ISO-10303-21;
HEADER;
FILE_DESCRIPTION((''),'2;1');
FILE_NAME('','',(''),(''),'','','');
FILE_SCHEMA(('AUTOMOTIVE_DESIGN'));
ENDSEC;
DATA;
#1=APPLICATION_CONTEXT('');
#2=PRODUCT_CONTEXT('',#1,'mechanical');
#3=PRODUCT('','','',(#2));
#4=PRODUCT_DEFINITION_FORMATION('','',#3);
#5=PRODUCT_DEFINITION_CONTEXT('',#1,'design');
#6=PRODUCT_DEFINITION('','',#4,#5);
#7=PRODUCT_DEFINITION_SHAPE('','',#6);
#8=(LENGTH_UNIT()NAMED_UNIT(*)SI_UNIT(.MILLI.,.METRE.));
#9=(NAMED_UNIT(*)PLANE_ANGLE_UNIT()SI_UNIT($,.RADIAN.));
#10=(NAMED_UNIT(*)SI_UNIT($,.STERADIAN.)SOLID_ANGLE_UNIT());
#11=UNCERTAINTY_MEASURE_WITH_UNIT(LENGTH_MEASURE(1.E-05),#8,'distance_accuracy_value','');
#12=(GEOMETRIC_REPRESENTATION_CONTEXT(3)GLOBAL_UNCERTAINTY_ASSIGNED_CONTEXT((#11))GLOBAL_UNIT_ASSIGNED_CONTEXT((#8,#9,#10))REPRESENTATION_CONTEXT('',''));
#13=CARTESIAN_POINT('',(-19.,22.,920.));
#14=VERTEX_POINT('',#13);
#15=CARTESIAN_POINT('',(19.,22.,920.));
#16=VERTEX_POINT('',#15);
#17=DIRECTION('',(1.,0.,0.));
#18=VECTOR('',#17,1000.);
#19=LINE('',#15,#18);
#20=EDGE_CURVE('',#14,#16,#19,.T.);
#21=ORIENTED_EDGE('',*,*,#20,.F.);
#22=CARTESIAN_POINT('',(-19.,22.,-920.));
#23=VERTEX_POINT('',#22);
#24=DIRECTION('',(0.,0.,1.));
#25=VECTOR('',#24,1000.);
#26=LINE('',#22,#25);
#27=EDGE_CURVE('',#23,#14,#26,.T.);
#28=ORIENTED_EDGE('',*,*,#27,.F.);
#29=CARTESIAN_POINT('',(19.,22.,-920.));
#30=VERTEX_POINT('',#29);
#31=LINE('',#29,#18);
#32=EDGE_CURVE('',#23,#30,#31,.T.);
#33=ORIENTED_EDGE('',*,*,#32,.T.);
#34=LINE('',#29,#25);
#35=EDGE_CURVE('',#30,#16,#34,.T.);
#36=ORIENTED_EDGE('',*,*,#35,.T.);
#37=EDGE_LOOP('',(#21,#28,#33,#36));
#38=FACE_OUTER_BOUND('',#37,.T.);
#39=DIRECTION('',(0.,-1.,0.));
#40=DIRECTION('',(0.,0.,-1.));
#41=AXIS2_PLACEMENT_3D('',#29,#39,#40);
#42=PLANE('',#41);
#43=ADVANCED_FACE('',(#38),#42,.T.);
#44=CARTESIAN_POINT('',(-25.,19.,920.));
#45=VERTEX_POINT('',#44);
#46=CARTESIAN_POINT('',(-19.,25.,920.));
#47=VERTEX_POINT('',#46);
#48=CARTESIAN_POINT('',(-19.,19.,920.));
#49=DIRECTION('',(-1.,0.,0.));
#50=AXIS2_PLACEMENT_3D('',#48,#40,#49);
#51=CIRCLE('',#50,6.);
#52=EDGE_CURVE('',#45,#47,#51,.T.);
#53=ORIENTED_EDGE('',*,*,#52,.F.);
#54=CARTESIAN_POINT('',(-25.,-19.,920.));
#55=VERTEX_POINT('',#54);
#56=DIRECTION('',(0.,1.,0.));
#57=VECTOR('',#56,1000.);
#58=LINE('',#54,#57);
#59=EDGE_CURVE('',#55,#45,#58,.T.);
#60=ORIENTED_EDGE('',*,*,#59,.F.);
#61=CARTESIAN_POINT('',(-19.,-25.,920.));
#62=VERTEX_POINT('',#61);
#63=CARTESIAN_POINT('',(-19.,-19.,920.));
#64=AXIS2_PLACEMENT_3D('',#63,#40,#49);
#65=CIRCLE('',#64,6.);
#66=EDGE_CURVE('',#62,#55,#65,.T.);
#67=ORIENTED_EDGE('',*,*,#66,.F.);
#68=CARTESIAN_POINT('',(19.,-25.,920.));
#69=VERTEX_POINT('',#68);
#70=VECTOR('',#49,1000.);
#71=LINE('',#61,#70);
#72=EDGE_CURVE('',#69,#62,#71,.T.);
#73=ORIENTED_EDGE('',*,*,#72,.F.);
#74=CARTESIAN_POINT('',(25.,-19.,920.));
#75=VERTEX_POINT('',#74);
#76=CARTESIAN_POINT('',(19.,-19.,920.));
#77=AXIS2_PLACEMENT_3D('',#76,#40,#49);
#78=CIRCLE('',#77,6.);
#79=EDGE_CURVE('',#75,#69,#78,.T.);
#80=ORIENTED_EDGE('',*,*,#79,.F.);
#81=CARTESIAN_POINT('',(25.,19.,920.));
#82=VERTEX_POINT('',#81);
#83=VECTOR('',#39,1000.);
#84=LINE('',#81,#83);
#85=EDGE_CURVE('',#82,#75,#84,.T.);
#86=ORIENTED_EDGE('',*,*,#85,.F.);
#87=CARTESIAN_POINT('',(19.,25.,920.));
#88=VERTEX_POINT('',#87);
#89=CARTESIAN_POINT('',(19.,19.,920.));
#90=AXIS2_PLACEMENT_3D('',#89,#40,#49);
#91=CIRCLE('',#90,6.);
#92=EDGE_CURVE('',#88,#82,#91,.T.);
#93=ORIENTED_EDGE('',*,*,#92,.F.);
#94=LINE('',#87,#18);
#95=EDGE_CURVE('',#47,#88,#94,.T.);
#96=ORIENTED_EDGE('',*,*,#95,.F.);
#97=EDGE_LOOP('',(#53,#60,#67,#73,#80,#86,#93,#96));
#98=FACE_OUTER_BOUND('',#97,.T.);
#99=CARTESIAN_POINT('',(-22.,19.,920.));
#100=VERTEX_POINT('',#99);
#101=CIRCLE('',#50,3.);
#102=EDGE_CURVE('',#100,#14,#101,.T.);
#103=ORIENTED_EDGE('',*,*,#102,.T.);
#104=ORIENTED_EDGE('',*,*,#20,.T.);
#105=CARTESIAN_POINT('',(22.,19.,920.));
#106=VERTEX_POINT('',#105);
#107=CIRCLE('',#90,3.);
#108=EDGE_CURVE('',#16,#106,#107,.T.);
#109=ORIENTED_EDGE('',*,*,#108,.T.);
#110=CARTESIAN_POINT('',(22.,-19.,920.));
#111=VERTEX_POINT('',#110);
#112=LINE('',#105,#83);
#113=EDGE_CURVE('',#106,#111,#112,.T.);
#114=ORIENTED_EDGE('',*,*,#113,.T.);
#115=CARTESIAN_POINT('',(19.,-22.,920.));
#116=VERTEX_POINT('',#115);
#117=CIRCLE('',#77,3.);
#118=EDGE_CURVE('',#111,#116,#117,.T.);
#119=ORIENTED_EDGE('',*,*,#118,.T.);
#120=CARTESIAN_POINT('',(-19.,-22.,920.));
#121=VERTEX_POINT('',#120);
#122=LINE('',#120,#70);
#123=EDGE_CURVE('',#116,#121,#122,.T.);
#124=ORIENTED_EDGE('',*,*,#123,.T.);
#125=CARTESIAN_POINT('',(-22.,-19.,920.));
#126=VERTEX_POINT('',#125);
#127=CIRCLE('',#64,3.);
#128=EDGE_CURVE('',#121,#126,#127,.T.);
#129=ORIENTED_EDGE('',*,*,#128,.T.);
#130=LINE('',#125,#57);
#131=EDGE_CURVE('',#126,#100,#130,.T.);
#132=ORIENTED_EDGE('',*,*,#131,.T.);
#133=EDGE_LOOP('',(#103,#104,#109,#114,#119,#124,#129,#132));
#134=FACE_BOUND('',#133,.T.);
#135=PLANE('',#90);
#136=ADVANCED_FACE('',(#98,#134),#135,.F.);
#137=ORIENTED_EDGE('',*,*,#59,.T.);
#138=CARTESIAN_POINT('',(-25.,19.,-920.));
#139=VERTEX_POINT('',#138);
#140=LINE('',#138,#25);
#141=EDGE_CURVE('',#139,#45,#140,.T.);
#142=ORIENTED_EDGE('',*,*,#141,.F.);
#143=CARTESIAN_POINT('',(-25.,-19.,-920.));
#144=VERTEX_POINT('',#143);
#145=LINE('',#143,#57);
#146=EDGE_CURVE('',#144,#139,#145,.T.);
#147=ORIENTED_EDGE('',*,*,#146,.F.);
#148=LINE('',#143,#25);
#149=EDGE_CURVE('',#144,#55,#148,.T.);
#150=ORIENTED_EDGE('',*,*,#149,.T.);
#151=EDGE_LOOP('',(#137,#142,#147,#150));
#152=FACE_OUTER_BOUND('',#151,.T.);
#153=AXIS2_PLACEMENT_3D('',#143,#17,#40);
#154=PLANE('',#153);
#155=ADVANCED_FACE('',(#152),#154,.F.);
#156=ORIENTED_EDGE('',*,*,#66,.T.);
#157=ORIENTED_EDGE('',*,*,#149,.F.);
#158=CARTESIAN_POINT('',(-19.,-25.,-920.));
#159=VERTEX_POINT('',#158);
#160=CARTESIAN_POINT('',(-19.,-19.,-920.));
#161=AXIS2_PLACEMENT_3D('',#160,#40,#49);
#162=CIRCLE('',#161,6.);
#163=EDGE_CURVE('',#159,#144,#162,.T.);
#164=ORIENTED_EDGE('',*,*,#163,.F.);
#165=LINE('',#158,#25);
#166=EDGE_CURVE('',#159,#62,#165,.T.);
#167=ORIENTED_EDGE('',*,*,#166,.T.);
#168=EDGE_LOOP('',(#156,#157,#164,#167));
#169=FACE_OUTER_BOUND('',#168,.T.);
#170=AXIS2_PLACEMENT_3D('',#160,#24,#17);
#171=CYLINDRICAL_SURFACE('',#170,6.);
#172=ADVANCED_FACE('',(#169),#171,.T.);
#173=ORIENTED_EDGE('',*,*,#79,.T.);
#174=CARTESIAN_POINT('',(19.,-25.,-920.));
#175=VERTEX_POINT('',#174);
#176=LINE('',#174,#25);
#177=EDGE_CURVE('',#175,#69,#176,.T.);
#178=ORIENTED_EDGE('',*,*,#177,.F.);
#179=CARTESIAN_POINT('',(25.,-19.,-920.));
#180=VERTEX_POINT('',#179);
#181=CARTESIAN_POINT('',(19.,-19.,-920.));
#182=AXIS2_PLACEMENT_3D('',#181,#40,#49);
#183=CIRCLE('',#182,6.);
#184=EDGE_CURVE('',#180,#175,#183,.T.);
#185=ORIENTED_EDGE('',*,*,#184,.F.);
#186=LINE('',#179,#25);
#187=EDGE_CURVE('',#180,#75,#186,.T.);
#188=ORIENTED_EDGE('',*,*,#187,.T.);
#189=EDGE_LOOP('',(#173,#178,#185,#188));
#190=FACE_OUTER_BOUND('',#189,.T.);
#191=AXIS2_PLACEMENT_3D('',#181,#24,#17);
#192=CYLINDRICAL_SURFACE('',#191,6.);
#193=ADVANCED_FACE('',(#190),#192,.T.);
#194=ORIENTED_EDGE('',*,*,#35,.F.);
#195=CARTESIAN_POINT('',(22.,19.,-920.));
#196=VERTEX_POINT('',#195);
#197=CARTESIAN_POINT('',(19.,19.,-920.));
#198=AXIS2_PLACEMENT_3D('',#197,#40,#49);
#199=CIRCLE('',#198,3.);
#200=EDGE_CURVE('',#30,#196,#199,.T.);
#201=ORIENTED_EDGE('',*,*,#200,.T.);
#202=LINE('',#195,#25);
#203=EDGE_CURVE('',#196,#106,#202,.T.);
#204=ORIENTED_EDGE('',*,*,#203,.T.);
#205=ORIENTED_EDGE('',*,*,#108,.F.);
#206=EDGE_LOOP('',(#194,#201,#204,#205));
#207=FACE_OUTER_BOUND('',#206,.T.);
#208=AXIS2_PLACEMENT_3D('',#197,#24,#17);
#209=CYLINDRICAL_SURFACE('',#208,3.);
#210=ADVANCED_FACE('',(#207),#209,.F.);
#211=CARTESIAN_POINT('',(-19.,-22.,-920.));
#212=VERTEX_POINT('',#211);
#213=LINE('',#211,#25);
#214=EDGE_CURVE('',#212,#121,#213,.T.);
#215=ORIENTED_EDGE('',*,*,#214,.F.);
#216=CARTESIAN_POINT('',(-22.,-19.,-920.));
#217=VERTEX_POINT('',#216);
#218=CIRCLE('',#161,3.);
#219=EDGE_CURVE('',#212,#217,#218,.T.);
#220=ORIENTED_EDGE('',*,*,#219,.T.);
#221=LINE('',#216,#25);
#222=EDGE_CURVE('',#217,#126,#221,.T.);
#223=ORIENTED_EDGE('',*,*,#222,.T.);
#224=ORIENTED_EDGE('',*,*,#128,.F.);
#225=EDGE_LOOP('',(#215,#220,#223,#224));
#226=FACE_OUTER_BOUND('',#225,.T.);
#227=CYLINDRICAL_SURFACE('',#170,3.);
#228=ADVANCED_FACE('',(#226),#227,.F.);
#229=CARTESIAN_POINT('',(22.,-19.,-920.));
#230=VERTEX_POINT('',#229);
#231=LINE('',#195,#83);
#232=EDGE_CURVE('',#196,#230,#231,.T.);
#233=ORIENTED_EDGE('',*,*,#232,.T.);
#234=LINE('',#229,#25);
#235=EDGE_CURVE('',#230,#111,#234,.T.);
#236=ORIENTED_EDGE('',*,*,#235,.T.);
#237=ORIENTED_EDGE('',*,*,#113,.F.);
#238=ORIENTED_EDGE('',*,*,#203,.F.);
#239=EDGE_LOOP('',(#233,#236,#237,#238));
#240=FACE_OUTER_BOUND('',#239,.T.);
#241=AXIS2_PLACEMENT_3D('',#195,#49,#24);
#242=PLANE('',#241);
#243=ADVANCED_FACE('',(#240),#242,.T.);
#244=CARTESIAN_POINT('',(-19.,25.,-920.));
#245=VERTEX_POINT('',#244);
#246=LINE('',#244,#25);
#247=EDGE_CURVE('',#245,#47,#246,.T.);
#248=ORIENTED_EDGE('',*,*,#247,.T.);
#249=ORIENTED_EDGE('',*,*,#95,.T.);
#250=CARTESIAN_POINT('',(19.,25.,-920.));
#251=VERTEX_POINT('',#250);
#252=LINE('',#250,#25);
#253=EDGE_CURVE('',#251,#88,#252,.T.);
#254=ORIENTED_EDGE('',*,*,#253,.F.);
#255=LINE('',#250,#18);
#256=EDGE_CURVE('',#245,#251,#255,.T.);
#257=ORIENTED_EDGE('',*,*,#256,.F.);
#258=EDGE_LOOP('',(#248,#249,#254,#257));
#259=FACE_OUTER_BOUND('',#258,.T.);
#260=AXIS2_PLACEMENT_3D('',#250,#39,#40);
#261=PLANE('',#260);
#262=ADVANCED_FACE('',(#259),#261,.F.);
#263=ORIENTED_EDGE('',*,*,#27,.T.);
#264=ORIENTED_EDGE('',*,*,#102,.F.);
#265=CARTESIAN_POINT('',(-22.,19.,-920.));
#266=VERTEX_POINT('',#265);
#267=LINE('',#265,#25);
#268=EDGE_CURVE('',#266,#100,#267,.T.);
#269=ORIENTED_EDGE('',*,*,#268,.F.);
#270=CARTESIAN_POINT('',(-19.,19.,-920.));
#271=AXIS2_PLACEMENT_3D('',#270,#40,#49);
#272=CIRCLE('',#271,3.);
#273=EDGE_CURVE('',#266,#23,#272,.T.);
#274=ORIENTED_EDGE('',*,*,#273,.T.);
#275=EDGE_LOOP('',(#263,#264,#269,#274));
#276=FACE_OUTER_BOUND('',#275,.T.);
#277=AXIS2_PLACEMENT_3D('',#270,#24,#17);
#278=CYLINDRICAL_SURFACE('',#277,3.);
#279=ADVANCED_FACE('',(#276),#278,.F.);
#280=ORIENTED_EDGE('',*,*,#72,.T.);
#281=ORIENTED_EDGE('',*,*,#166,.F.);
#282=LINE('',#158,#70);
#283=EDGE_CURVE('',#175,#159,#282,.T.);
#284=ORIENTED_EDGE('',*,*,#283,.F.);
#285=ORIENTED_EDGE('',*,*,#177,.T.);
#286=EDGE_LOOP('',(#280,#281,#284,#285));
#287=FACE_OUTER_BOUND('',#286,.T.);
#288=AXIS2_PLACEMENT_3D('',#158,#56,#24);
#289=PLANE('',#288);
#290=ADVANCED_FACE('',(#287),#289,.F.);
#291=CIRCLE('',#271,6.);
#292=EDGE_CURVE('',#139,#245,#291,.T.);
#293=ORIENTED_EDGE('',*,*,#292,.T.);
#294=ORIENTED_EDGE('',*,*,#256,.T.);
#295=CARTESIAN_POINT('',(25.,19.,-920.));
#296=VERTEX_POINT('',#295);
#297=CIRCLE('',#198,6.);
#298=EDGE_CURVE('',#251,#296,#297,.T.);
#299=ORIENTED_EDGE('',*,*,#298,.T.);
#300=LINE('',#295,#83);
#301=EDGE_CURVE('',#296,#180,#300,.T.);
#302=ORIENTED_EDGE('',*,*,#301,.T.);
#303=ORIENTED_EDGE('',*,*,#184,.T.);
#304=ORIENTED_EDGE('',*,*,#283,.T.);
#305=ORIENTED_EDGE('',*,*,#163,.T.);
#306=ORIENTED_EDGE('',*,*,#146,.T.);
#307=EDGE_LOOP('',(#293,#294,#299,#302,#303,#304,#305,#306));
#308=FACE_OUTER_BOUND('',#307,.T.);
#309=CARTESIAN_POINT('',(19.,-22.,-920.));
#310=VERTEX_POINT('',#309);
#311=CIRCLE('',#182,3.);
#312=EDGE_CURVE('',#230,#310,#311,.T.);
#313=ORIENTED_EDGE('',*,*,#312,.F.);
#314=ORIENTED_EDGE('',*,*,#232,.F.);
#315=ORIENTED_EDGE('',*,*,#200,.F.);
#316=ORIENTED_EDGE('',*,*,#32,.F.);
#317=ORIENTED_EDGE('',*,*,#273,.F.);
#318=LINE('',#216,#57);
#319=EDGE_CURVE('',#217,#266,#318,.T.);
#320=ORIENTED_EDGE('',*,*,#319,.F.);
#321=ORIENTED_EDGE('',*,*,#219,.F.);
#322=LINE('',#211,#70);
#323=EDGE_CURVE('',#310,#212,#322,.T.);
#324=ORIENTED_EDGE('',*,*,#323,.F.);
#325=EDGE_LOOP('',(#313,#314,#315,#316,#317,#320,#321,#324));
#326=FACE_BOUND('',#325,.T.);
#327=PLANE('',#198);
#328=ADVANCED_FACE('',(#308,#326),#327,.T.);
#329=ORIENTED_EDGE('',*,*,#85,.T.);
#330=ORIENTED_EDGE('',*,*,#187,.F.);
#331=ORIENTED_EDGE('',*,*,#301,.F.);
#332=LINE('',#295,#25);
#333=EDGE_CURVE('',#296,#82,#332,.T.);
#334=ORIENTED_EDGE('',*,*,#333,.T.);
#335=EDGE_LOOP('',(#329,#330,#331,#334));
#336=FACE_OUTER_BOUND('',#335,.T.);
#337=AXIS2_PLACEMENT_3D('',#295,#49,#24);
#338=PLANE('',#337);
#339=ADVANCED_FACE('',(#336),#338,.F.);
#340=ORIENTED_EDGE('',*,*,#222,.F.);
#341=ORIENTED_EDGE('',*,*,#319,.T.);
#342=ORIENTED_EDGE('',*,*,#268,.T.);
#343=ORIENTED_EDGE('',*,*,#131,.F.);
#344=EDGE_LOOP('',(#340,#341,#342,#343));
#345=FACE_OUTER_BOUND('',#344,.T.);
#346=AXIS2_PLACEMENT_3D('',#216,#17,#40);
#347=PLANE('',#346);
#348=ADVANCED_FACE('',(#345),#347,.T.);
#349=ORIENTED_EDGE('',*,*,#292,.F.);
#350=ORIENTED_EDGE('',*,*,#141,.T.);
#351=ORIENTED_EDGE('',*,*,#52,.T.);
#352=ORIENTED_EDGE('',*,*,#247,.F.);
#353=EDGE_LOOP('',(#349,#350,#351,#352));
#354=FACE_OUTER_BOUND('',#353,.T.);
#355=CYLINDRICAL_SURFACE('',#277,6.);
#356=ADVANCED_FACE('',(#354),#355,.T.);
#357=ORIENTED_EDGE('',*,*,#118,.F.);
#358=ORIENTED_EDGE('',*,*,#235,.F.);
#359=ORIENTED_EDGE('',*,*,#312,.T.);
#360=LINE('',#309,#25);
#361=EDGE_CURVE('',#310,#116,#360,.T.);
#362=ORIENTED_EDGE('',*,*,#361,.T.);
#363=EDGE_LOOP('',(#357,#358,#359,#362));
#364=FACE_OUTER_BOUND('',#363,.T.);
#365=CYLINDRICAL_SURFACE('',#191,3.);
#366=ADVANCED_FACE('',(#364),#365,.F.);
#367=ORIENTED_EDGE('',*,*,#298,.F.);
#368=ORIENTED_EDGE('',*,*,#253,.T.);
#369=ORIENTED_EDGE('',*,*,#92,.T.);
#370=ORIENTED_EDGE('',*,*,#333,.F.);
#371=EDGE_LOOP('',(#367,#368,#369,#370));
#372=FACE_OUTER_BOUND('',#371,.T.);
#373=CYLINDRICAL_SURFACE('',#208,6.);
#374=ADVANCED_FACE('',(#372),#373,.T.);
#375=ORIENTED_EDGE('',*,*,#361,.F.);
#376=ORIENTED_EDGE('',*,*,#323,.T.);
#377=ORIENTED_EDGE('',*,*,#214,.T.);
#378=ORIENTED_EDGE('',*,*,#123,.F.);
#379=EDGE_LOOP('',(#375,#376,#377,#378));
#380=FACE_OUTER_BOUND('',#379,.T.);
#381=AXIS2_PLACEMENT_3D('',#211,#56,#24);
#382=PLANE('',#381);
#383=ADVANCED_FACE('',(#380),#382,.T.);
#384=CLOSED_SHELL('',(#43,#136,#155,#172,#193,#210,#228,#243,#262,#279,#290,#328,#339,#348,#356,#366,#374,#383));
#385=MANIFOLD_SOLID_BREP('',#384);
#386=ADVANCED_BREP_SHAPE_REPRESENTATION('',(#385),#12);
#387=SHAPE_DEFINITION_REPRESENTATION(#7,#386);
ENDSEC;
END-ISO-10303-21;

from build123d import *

# Parameters (mm, degrees)
GB_6728_1986_050_X_50_X_3_1_DEPTH = 1840


with BuildPart() as part:
    # Sketch1 → Gb／6728-1986方形空心型钢 050 X 50 X 3(1) (new body)
    with BuildSketch(Plane.YX.offset(-920)):
        with BuildLine():
            Line((-19, -25), (19, -25))
            ThreePointArc((19, -25), (23.242640687, -23.242640687), (25, -19))
            Line((25, -19), (25, 19))
            ThreePointArc((25, 19), (23.242640687, 23.242640687), (19, 25))
            Line((19, 25), (-19, 25))
            ThreePointArc((-19, 25), (-23.242640687, 23.242640687), (-25, 19))
            Line((-25, 19), (-25, -19))
            ThreePointArc((-25, -19), (-23.242640687, -23.242640687), (-19, -25))
        make_face()
        with BuildLine():
            Line((-19, -22), (19, -22))
            ThreePointArc((19, -22), (21.121320344, -21.121320344), (22, -19))
            Line((22, -19), (22, 19))
            ThreePointArc((22, 19), (21.121320344, 21.121320344), (19, 22))
            Line((19, 22), (-19, 22))
            ThreePointArc((-19, 22), (-21.121320344, 21.121320344), (-22, 19))
            Line((-22, 19), (-22, -19))
            ThreePointArc((-22, -19), (-21.121320344, -21.121320344), (-19, -22))
        make_face(mode=Mode.SUBTRACT)
    extrude(amount=GB_6728_1986_050_X_50_X_3_1_DEPTH)


solid = part.part
